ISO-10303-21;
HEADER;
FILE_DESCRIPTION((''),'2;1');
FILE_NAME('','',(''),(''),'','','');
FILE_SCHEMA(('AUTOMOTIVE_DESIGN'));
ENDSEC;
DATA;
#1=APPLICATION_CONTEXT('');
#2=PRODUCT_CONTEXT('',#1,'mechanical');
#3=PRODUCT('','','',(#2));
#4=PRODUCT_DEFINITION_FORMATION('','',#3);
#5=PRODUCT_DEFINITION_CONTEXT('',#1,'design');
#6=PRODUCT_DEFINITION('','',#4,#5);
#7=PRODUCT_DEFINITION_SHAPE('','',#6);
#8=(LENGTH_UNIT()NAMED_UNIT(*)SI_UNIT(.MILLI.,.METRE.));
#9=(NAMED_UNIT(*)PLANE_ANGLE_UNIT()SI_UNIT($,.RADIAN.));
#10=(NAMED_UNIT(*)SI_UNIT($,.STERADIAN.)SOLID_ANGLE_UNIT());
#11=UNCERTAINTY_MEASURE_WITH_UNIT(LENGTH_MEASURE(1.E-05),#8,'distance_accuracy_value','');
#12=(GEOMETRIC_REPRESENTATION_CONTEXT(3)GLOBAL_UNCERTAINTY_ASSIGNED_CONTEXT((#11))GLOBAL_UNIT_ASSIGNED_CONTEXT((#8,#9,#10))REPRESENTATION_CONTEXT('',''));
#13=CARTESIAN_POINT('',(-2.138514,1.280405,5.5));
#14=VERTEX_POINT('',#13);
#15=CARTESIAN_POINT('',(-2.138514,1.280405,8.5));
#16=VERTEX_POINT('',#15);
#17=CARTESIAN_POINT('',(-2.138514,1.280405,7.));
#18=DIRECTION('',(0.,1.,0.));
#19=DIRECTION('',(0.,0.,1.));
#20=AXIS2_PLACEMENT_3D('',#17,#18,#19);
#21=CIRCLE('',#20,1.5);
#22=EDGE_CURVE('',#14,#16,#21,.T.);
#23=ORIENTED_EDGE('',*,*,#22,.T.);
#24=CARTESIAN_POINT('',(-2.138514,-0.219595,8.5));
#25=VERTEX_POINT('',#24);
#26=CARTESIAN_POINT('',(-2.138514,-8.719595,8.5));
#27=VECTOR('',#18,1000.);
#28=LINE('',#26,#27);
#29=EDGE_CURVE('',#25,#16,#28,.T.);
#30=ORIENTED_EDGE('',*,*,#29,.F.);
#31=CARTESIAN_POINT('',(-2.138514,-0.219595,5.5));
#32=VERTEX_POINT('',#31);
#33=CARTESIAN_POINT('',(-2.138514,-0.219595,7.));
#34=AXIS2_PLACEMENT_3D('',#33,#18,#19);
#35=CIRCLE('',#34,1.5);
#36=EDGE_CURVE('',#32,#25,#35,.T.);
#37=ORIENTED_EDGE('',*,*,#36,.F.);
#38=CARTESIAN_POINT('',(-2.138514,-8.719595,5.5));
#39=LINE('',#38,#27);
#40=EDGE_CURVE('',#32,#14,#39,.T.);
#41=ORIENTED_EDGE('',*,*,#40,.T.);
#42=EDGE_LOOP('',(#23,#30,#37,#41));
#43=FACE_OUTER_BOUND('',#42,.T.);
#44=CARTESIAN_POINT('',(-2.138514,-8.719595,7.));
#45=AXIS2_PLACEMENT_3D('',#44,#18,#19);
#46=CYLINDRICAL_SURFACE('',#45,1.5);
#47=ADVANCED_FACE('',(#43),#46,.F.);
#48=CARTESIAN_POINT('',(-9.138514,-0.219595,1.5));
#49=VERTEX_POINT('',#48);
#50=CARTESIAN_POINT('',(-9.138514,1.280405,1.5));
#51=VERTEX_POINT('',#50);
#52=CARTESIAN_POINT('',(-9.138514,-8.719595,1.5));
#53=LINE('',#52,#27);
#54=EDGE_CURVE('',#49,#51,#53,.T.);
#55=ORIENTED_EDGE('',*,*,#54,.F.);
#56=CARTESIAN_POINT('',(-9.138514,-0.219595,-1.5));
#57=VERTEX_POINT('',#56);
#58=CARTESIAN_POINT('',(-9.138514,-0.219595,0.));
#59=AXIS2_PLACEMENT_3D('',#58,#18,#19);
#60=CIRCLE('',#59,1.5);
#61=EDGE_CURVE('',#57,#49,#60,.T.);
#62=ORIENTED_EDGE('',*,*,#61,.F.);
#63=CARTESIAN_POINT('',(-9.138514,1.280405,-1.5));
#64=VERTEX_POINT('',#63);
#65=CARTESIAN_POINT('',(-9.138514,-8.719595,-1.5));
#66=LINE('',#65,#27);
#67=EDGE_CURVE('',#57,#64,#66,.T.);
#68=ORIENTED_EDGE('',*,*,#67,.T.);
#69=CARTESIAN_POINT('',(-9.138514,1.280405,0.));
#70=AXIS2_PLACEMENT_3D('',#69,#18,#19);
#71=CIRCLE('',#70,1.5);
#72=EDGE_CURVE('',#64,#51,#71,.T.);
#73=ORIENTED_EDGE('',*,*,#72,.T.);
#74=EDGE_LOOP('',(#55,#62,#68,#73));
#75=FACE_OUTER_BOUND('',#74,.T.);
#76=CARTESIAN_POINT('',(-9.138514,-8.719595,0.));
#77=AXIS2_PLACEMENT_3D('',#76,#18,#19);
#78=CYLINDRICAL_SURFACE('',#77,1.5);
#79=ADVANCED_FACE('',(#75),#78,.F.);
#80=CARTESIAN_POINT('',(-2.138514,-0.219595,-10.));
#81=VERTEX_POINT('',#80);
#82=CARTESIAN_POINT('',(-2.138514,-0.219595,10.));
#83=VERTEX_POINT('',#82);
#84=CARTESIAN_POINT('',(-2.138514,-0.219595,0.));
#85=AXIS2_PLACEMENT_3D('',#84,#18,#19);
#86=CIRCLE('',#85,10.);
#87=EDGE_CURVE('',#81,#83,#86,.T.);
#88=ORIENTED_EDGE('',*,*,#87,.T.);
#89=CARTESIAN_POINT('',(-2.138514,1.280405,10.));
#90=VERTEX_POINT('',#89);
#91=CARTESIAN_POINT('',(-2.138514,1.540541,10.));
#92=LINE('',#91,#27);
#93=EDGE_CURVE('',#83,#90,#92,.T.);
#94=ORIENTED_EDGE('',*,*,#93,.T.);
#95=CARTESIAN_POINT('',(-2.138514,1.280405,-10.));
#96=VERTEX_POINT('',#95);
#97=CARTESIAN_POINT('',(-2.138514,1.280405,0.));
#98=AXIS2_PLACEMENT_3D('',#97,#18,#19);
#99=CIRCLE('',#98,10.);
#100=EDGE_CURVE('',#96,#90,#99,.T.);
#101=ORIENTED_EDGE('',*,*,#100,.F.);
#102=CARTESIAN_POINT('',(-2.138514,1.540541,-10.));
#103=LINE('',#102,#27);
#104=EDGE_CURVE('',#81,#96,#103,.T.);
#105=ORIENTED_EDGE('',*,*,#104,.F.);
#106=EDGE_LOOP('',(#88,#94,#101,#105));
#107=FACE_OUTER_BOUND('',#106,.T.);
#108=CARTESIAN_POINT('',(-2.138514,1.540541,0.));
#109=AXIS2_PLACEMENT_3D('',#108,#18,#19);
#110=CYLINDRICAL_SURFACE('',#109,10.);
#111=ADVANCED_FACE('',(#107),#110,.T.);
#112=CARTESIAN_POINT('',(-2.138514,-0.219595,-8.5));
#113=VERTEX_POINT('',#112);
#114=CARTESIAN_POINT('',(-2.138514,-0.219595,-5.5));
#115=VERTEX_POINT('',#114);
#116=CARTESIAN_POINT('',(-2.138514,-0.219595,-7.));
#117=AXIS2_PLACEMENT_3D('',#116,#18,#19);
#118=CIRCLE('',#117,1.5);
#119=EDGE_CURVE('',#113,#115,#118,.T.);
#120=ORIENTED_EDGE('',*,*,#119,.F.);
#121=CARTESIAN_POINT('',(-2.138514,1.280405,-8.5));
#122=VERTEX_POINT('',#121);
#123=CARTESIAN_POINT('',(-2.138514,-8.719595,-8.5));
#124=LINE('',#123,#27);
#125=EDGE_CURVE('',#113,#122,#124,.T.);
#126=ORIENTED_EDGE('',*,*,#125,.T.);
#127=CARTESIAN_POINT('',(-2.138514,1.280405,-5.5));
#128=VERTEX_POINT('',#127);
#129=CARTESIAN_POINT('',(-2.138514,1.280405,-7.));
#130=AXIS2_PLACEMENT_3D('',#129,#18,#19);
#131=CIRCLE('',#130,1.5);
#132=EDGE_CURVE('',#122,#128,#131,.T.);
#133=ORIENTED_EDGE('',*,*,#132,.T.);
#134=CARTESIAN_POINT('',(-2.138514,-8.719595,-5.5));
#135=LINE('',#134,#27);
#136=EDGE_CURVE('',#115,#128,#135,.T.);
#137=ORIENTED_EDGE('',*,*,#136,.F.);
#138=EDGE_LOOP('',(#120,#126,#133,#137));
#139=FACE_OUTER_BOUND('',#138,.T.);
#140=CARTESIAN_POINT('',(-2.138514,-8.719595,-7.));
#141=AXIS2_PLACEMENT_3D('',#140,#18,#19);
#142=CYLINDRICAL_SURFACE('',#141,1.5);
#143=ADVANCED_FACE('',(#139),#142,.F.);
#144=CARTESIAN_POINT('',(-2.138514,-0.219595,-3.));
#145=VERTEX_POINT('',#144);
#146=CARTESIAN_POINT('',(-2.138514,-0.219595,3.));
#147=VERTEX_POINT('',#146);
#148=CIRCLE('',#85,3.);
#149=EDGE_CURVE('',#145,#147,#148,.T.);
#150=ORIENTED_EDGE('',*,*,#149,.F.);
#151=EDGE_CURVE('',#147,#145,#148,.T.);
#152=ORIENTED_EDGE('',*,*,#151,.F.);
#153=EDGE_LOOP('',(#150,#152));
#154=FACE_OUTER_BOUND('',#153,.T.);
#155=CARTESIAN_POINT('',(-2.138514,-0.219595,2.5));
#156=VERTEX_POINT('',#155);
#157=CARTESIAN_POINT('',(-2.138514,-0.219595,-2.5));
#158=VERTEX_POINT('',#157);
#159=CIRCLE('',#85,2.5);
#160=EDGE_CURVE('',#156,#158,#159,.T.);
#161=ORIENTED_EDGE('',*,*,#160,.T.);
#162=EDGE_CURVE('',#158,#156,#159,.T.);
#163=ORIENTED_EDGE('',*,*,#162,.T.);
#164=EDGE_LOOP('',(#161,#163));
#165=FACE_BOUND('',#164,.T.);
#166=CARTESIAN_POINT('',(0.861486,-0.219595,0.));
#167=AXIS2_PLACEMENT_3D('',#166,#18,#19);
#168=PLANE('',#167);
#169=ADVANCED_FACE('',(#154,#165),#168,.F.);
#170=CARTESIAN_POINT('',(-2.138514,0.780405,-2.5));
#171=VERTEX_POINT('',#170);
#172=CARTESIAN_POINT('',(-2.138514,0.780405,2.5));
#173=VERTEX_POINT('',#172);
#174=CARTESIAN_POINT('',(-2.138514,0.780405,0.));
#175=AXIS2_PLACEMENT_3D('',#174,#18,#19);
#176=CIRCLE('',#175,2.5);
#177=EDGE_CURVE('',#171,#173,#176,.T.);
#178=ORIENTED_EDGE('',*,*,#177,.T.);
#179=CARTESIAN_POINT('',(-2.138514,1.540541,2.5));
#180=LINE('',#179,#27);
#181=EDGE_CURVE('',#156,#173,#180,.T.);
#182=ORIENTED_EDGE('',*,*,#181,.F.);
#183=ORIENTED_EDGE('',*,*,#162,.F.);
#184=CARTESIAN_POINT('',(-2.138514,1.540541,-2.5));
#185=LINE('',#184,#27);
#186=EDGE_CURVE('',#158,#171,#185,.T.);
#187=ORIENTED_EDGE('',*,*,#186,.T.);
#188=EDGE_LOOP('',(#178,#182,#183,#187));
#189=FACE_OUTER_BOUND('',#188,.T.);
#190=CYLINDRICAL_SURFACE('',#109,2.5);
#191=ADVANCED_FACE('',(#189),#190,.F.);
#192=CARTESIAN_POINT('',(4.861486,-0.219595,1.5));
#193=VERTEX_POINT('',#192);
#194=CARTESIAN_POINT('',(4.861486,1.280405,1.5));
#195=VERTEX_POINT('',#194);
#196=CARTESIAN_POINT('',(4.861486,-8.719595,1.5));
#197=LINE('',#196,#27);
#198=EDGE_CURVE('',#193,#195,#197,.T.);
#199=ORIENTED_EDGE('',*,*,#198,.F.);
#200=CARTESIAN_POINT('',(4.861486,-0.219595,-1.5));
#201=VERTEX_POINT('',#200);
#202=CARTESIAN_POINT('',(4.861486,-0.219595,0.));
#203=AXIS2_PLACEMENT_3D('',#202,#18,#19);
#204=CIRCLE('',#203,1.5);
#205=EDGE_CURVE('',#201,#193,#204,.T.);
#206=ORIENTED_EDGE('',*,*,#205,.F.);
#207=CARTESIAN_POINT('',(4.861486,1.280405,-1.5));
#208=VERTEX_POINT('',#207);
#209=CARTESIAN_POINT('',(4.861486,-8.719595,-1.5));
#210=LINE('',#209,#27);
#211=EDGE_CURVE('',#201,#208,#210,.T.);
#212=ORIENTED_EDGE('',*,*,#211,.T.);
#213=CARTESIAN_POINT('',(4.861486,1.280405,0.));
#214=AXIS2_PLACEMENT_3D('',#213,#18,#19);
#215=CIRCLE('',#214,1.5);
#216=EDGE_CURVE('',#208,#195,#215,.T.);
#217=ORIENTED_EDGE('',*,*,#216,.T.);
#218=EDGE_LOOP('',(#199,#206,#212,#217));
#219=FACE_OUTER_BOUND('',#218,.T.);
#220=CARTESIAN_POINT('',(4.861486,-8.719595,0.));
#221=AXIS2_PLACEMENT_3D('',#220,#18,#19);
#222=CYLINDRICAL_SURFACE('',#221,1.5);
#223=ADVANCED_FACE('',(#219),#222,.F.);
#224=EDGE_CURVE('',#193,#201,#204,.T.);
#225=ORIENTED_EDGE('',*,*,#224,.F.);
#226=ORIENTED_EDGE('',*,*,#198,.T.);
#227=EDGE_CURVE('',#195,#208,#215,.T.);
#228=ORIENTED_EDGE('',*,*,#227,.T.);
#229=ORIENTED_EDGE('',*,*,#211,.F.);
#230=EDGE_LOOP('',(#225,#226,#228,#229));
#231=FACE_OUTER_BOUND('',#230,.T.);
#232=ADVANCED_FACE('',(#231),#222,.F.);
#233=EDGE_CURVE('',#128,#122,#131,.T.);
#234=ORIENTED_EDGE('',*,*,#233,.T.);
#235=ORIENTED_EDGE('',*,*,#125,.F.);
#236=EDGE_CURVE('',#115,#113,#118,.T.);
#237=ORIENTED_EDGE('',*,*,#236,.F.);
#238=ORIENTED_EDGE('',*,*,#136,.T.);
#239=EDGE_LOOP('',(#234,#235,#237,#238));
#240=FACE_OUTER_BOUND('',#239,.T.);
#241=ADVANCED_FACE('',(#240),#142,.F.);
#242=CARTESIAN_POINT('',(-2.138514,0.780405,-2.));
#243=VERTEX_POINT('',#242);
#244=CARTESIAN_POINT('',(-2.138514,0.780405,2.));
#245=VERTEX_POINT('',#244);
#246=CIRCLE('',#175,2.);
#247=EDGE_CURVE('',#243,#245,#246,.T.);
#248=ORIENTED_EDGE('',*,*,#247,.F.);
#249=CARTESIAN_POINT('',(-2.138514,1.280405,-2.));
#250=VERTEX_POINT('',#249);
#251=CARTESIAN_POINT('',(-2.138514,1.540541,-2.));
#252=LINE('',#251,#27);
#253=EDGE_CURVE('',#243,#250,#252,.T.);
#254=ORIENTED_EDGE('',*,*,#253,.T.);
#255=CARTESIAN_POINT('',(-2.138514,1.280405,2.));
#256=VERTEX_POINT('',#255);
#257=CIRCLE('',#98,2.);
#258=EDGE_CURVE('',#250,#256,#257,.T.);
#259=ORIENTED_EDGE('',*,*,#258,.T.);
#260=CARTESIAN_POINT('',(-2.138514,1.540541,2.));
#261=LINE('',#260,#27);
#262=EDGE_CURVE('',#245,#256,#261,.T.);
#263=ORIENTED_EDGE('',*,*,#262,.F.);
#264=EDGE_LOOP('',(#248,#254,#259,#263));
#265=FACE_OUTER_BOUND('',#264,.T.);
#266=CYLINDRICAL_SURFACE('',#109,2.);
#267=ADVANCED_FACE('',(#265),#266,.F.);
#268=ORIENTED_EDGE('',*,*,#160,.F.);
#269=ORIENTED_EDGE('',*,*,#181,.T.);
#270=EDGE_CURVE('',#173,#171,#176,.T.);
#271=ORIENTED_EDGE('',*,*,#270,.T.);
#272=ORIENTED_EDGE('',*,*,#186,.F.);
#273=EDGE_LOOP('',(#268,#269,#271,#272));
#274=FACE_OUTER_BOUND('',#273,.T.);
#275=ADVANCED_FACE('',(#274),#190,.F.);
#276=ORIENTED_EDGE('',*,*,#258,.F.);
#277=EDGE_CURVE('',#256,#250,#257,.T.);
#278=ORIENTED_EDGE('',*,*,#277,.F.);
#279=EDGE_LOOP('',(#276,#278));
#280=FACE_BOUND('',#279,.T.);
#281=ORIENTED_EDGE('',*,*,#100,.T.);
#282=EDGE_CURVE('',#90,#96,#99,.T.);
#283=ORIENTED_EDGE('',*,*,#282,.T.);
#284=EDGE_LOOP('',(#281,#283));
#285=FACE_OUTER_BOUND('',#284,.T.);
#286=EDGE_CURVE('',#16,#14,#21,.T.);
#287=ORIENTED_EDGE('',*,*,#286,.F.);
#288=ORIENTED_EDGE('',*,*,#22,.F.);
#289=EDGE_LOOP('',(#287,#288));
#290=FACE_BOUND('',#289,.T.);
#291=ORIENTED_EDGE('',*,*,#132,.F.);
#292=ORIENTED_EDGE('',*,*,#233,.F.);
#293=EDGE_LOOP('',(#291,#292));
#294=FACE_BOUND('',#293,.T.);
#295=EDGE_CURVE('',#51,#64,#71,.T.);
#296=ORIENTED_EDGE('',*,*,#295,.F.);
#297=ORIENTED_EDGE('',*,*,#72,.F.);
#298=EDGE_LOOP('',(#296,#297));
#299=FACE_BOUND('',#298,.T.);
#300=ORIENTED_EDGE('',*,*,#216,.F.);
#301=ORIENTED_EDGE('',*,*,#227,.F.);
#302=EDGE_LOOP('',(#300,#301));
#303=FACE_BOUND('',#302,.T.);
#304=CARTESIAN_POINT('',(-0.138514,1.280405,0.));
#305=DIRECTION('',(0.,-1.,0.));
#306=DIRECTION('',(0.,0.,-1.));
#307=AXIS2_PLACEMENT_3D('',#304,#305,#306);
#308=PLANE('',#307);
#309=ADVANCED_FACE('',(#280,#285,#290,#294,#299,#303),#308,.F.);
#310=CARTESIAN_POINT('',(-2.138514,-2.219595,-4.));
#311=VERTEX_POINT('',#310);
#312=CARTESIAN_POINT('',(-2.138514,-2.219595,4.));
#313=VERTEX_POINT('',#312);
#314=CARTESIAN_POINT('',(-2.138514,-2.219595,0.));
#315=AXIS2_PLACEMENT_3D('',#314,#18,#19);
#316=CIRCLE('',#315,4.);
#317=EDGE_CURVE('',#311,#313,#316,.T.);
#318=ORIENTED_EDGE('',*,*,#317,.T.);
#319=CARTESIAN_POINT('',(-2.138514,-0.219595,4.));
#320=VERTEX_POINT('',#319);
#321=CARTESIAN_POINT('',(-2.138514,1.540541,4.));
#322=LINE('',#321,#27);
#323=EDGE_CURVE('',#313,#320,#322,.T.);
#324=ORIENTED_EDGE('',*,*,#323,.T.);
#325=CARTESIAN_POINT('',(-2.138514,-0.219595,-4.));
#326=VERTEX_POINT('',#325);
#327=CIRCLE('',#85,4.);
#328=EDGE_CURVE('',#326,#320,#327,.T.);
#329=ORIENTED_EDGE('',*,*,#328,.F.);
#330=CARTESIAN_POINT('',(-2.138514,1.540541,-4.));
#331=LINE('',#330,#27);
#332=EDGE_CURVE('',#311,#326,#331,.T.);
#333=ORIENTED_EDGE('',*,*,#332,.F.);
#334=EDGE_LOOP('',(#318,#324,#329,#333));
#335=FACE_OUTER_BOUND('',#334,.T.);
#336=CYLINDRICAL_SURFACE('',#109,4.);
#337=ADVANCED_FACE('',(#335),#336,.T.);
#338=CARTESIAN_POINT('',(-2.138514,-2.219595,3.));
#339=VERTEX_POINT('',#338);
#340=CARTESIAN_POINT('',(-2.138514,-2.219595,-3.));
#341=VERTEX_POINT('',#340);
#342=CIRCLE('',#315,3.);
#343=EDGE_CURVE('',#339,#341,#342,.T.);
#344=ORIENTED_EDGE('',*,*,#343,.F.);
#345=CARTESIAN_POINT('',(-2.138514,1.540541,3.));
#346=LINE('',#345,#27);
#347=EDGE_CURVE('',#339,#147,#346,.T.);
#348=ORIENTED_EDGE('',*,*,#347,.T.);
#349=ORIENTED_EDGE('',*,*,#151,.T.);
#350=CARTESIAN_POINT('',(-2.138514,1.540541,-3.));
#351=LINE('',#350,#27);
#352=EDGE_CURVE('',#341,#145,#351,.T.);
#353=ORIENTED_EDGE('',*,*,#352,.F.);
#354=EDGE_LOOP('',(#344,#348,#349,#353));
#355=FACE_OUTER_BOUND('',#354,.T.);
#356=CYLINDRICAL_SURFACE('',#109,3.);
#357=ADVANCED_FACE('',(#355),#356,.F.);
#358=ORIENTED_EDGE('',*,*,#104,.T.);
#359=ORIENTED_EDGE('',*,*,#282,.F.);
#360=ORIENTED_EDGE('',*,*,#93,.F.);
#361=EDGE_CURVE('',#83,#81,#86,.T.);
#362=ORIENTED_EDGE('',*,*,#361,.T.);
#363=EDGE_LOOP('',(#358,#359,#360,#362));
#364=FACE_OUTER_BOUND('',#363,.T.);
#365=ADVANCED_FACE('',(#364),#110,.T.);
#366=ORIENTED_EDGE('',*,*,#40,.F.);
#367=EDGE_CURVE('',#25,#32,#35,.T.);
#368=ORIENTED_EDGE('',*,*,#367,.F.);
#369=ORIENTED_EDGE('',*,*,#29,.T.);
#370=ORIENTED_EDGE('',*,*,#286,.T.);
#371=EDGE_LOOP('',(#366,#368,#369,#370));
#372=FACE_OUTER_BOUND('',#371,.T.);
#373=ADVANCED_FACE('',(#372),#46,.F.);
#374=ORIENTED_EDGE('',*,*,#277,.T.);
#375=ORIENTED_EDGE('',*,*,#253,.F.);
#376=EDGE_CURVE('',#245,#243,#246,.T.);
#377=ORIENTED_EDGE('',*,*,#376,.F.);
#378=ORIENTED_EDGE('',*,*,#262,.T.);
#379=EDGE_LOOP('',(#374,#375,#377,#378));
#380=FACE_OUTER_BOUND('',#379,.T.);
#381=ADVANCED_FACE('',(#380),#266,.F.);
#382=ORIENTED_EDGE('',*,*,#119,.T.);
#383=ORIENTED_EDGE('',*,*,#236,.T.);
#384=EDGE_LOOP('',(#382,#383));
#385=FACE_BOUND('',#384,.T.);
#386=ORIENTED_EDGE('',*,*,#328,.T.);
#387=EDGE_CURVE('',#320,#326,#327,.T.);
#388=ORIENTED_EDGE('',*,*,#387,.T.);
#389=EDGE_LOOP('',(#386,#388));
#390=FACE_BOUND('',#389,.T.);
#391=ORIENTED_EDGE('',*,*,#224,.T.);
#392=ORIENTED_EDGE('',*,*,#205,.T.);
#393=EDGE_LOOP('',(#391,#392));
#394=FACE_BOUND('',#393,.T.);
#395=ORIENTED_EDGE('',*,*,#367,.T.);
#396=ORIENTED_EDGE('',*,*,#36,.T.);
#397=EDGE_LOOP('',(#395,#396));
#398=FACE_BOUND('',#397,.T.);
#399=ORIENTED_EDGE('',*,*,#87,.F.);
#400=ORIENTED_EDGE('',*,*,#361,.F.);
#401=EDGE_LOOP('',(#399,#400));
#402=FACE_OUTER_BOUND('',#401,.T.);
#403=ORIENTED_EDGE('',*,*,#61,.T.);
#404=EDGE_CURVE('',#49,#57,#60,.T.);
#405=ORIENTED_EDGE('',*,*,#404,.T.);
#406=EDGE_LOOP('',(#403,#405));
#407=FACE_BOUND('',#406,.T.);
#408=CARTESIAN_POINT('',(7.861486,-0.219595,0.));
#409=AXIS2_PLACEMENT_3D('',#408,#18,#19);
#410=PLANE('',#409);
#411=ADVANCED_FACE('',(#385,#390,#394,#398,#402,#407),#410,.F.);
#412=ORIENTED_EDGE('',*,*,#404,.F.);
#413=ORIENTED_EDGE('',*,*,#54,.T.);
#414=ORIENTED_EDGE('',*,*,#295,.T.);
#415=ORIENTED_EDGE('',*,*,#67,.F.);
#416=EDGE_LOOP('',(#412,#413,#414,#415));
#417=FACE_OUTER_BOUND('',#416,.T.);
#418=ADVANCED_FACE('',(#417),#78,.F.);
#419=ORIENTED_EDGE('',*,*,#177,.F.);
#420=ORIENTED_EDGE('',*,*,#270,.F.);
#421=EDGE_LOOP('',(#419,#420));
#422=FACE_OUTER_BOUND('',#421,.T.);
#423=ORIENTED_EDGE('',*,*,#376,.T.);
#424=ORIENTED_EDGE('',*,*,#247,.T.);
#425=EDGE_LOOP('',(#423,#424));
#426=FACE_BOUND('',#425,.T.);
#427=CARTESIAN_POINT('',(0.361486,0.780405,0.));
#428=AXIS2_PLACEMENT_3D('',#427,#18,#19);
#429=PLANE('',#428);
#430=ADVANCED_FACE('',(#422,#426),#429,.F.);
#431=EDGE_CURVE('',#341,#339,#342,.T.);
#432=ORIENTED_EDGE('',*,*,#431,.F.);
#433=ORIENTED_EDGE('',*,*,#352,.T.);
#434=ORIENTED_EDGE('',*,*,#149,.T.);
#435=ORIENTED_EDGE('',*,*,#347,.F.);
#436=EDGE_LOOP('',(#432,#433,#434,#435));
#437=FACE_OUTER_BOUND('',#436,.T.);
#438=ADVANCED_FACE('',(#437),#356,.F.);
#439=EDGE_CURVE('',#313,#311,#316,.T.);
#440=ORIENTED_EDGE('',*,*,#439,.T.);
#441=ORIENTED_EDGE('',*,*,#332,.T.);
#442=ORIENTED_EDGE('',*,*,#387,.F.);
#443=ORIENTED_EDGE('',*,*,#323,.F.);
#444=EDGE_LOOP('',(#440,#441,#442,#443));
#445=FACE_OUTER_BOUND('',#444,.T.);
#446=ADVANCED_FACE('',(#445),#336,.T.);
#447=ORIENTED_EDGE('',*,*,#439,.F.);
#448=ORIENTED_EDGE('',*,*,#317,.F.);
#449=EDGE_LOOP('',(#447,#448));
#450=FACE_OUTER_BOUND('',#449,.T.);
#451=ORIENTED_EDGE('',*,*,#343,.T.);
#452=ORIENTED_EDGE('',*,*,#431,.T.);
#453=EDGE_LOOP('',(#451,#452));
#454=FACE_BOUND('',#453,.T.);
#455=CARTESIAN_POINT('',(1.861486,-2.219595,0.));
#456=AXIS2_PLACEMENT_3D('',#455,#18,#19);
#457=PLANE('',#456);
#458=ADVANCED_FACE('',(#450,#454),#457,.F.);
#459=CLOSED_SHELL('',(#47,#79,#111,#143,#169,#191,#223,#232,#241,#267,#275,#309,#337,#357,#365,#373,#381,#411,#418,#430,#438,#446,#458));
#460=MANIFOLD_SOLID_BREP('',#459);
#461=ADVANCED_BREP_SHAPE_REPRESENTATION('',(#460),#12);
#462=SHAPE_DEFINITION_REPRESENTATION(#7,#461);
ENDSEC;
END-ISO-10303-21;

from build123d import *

# Parameters (mm, degrees)
SKETCH2_R          = 1.5
CUT_EXTRUDE1_DEPTH = 10


with BuildPart() as part:
    # Sketch1 → Revolve1 (revolve)
    with BuildSketch(Plane.XY, mode=Mode.PRIVATE) as revolve1_sk:
        Polygon((-0.138513514, 1.280405405), (7.861486486, 1.280405405), (7.861486486, -0.219594595), (1.861486486, -0.219594595), (1.861486486, -1.019594595), (1.861486486, -2.219594595), (0.861486486, -2.219594595), (0.861486486, -0.219594595), (0.361486486, -0.219594595), (0.361486486, 0.780405405), (-0.138513514, 0.780405405), align=None)
    revolve(revolve1_sk.sketch.rotate(Axis((-2.138513514, 1.540540541, 0), (0, -1, 0)), 90), axis=Axis((-2.138513514, 1.540540541, 0), (0, -1, 0)))

    # Sketch2 → Cut-Extrude1 (cut)
    with BuildSketch(Plane(origin=(0, 1.280405405, 0), x_dir=(1, 0, 0), z_dir=(0, 1, 0))):
        with Locations(Location((-2.138513514, 7, 0), (0, 0, 270))):
            Circle(SKETCH2_R)
        with Locations(Location((4.861486486, 0, 0), (0, 0, 270))):
            Circle(SKETCH2_R)
        with Locations(Location((-2.138513514, -7, 0), (0, 0, 269.999999999))):
            Circle(SKETCH2_R)
        with Locations(Location((-9.138513514, 0, 0), (0, 0, 270))):
            Circle(SKETCH2_R)
    extrude(amount=-CUT_EXTRUDE1_DEPTH, mode=Mode.SUBTRACT)


solid = part.part
